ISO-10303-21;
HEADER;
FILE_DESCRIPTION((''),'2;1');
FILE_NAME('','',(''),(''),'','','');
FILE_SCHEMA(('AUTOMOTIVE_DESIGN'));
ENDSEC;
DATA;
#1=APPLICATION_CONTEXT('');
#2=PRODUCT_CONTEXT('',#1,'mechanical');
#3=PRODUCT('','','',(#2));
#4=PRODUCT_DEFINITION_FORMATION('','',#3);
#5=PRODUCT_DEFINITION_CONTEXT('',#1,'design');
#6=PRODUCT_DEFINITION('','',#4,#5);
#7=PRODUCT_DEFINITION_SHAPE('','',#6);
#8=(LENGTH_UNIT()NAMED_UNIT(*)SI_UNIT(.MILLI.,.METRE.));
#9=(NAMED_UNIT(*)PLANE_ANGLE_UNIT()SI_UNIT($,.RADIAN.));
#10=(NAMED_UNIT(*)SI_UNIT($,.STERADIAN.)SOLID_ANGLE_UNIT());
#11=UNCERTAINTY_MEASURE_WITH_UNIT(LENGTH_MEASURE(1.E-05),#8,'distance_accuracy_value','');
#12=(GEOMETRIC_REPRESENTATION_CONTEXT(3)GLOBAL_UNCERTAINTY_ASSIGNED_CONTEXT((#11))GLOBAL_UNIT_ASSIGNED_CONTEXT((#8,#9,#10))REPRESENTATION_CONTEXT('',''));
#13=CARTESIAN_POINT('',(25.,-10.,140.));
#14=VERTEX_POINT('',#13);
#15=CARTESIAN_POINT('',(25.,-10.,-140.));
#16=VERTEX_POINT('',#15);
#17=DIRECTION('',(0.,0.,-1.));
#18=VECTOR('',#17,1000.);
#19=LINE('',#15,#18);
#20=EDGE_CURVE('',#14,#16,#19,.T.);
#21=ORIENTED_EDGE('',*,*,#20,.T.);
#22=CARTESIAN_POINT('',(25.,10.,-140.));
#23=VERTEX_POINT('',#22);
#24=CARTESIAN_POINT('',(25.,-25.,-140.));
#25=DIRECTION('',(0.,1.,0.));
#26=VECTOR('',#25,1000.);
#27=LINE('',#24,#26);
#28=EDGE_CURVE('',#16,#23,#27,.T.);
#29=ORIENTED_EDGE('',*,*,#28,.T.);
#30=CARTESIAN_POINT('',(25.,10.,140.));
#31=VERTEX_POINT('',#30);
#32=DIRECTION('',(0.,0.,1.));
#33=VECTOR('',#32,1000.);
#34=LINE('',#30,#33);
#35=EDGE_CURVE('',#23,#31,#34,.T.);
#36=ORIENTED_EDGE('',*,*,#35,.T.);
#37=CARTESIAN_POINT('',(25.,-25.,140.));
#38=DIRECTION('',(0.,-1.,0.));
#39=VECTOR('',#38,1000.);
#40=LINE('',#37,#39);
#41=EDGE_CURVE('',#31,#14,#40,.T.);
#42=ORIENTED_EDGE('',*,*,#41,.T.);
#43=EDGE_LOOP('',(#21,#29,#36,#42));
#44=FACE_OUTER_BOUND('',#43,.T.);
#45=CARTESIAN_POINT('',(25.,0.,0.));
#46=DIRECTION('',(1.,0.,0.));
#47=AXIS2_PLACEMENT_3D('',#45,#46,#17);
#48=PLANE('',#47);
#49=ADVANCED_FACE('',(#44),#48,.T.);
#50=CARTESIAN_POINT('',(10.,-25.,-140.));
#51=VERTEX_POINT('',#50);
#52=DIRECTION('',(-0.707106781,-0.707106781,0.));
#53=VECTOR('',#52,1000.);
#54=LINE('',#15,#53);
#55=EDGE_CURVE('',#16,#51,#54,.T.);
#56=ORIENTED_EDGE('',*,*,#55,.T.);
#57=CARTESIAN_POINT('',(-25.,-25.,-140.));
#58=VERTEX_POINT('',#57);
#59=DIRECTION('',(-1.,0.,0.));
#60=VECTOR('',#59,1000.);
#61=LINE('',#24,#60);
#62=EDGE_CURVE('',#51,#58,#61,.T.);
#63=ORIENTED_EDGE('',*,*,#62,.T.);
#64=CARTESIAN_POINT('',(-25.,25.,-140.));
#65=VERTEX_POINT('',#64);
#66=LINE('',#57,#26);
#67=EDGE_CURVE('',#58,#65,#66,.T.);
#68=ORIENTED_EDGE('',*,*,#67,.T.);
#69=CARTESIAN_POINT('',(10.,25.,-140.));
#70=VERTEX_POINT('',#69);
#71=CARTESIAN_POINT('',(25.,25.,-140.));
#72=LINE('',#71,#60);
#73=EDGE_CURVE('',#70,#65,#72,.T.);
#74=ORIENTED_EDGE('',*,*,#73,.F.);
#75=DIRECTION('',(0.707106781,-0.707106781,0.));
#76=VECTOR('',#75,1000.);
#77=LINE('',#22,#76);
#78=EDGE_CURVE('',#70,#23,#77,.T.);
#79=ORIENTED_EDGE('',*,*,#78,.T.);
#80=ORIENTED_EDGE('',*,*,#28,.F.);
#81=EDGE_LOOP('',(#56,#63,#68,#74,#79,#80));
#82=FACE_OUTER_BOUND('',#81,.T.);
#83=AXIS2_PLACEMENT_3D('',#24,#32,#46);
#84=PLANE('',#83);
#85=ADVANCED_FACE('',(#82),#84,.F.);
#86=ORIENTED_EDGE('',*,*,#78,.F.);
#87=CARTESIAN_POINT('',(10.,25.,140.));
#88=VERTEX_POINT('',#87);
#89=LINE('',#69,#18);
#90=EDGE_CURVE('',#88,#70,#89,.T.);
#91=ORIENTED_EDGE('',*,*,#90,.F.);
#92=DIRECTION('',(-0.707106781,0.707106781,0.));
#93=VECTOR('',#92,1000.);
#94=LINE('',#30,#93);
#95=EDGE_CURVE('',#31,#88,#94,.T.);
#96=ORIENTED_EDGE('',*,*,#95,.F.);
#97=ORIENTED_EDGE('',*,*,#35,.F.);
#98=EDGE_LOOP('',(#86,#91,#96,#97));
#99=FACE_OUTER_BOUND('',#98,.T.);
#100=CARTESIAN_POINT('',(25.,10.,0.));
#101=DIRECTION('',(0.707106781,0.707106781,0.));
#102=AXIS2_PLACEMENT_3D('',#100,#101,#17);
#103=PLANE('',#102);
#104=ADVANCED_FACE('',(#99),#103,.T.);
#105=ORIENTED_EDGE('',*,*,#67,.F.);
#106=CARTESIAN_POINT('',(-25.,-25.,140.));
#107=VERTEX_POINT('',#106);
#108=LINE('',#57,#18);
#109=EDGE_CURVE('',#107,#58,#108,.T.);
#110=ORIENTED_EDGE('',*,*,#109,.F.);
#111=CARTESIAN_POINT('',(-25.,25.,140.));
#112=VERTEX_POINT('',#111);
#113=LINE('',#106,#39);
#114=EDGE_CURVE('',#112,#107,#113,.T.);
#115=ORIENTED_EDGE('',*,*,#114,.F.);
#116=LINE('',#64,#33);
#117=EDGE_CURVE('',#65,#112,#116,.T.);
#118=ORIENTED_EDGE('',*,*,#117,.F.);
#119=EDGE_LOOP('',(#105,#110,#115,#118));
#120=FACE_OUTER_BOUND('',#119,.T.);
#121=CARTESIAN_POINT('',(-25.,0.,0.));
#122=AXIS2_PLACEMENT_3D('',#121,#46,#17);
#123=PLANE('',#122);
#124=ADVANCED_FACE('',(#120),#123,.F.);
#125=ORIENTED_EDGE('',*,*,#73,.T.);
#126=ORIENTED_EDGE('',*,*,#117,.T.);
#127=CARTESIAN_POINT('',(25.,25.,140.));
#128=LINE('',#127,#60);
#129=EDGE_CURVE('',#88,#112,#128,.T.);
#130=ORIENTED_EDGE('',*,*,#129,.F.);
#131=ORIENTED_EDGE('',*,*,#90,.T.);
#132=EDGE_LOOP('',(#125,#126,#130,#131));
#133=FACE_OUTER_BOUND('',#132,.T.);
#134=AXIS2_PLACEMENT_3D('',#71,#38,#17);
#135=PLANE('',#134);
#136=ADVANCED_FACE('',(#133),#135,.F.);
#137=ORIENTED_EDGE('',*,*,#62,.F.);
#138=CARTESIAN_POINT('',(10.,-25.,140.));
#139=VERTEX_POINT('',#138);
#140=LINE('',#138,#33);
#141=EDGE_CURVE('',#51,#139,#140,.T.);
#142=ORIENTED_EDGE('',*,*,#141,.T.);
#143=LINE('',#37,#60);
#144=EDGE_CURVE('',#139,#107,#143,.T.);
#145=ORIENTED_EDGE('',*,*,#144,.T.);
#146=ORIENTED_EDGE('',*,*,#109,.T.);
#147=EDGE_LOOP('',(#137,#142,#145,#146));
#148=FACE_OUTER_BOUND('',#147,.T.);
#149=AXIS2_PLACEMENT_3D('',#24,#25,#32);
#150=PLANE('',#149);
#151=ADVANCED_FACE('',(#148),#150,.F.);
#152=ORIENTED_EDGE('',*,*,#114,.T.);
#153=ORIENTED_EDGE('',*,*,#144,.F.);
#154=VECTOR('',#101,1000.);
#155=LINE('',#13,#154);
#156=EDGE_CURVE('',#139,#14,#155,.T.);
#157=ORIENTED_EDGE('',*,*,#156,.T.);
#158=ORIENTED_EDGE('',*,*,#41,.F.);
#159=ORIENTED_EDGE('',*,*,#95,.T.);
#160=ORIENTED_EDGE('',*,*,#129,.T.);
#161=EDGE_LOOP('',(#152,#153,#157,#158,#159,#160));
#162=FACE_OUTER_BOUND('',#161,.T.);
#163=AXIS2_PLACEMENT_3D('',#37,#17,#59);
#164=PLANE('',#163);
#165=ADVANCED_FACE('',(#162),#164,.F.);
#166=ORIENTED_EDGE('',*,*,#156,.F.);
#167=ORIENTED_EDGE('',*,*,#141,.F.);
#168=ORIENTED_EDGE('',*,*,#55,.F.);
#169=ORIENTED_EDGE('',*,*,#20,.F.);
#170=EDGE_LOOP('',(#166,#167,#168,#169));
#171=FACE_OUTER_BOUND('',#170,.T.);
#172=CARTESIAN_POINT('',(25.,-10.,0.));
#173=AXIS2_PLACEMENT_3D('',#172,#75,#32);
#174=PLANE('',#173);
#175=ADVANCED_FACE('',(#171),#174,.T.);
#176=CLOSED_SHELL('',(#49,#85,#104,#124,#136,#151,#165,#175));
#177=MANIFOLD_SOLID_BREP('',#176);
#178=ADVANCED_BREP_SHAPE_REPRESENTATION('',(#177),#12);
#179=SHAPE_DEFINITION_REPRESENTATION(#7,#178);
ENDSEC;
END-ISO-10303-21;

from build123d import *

# Parameters (mm, degrees)
SKETCH1_W           = 280
SKETCH1_H           = 50
BOSS_EXTRUDE1_DEPTH = 25
CHAMFER1_SIZE       = 15


with BuildPart() as part:
    # Sketch1 → Boss-Extrude1 (new, symmetric)
    with BuildSketch(Plane(origin=(0, 0, 0), x_dir=(0, 0, -1), z_dir=(1, 0, 0))):
        Rectangle(SKETCH1_W, SKETCH1_H)
    extrude(amount=BOSS_EXTRUDE1_DEPTH, both=True)

    # Chamfer1
    chamfer1_edges = [part.edges().sort_by_distance(p)[0] for p in [
        (25, 25, 0),
        (25, -25, 0),
    ]]
    chamfer(chamfer1_edges, length=CHAMFER1_SIZE)


solid = part.part
